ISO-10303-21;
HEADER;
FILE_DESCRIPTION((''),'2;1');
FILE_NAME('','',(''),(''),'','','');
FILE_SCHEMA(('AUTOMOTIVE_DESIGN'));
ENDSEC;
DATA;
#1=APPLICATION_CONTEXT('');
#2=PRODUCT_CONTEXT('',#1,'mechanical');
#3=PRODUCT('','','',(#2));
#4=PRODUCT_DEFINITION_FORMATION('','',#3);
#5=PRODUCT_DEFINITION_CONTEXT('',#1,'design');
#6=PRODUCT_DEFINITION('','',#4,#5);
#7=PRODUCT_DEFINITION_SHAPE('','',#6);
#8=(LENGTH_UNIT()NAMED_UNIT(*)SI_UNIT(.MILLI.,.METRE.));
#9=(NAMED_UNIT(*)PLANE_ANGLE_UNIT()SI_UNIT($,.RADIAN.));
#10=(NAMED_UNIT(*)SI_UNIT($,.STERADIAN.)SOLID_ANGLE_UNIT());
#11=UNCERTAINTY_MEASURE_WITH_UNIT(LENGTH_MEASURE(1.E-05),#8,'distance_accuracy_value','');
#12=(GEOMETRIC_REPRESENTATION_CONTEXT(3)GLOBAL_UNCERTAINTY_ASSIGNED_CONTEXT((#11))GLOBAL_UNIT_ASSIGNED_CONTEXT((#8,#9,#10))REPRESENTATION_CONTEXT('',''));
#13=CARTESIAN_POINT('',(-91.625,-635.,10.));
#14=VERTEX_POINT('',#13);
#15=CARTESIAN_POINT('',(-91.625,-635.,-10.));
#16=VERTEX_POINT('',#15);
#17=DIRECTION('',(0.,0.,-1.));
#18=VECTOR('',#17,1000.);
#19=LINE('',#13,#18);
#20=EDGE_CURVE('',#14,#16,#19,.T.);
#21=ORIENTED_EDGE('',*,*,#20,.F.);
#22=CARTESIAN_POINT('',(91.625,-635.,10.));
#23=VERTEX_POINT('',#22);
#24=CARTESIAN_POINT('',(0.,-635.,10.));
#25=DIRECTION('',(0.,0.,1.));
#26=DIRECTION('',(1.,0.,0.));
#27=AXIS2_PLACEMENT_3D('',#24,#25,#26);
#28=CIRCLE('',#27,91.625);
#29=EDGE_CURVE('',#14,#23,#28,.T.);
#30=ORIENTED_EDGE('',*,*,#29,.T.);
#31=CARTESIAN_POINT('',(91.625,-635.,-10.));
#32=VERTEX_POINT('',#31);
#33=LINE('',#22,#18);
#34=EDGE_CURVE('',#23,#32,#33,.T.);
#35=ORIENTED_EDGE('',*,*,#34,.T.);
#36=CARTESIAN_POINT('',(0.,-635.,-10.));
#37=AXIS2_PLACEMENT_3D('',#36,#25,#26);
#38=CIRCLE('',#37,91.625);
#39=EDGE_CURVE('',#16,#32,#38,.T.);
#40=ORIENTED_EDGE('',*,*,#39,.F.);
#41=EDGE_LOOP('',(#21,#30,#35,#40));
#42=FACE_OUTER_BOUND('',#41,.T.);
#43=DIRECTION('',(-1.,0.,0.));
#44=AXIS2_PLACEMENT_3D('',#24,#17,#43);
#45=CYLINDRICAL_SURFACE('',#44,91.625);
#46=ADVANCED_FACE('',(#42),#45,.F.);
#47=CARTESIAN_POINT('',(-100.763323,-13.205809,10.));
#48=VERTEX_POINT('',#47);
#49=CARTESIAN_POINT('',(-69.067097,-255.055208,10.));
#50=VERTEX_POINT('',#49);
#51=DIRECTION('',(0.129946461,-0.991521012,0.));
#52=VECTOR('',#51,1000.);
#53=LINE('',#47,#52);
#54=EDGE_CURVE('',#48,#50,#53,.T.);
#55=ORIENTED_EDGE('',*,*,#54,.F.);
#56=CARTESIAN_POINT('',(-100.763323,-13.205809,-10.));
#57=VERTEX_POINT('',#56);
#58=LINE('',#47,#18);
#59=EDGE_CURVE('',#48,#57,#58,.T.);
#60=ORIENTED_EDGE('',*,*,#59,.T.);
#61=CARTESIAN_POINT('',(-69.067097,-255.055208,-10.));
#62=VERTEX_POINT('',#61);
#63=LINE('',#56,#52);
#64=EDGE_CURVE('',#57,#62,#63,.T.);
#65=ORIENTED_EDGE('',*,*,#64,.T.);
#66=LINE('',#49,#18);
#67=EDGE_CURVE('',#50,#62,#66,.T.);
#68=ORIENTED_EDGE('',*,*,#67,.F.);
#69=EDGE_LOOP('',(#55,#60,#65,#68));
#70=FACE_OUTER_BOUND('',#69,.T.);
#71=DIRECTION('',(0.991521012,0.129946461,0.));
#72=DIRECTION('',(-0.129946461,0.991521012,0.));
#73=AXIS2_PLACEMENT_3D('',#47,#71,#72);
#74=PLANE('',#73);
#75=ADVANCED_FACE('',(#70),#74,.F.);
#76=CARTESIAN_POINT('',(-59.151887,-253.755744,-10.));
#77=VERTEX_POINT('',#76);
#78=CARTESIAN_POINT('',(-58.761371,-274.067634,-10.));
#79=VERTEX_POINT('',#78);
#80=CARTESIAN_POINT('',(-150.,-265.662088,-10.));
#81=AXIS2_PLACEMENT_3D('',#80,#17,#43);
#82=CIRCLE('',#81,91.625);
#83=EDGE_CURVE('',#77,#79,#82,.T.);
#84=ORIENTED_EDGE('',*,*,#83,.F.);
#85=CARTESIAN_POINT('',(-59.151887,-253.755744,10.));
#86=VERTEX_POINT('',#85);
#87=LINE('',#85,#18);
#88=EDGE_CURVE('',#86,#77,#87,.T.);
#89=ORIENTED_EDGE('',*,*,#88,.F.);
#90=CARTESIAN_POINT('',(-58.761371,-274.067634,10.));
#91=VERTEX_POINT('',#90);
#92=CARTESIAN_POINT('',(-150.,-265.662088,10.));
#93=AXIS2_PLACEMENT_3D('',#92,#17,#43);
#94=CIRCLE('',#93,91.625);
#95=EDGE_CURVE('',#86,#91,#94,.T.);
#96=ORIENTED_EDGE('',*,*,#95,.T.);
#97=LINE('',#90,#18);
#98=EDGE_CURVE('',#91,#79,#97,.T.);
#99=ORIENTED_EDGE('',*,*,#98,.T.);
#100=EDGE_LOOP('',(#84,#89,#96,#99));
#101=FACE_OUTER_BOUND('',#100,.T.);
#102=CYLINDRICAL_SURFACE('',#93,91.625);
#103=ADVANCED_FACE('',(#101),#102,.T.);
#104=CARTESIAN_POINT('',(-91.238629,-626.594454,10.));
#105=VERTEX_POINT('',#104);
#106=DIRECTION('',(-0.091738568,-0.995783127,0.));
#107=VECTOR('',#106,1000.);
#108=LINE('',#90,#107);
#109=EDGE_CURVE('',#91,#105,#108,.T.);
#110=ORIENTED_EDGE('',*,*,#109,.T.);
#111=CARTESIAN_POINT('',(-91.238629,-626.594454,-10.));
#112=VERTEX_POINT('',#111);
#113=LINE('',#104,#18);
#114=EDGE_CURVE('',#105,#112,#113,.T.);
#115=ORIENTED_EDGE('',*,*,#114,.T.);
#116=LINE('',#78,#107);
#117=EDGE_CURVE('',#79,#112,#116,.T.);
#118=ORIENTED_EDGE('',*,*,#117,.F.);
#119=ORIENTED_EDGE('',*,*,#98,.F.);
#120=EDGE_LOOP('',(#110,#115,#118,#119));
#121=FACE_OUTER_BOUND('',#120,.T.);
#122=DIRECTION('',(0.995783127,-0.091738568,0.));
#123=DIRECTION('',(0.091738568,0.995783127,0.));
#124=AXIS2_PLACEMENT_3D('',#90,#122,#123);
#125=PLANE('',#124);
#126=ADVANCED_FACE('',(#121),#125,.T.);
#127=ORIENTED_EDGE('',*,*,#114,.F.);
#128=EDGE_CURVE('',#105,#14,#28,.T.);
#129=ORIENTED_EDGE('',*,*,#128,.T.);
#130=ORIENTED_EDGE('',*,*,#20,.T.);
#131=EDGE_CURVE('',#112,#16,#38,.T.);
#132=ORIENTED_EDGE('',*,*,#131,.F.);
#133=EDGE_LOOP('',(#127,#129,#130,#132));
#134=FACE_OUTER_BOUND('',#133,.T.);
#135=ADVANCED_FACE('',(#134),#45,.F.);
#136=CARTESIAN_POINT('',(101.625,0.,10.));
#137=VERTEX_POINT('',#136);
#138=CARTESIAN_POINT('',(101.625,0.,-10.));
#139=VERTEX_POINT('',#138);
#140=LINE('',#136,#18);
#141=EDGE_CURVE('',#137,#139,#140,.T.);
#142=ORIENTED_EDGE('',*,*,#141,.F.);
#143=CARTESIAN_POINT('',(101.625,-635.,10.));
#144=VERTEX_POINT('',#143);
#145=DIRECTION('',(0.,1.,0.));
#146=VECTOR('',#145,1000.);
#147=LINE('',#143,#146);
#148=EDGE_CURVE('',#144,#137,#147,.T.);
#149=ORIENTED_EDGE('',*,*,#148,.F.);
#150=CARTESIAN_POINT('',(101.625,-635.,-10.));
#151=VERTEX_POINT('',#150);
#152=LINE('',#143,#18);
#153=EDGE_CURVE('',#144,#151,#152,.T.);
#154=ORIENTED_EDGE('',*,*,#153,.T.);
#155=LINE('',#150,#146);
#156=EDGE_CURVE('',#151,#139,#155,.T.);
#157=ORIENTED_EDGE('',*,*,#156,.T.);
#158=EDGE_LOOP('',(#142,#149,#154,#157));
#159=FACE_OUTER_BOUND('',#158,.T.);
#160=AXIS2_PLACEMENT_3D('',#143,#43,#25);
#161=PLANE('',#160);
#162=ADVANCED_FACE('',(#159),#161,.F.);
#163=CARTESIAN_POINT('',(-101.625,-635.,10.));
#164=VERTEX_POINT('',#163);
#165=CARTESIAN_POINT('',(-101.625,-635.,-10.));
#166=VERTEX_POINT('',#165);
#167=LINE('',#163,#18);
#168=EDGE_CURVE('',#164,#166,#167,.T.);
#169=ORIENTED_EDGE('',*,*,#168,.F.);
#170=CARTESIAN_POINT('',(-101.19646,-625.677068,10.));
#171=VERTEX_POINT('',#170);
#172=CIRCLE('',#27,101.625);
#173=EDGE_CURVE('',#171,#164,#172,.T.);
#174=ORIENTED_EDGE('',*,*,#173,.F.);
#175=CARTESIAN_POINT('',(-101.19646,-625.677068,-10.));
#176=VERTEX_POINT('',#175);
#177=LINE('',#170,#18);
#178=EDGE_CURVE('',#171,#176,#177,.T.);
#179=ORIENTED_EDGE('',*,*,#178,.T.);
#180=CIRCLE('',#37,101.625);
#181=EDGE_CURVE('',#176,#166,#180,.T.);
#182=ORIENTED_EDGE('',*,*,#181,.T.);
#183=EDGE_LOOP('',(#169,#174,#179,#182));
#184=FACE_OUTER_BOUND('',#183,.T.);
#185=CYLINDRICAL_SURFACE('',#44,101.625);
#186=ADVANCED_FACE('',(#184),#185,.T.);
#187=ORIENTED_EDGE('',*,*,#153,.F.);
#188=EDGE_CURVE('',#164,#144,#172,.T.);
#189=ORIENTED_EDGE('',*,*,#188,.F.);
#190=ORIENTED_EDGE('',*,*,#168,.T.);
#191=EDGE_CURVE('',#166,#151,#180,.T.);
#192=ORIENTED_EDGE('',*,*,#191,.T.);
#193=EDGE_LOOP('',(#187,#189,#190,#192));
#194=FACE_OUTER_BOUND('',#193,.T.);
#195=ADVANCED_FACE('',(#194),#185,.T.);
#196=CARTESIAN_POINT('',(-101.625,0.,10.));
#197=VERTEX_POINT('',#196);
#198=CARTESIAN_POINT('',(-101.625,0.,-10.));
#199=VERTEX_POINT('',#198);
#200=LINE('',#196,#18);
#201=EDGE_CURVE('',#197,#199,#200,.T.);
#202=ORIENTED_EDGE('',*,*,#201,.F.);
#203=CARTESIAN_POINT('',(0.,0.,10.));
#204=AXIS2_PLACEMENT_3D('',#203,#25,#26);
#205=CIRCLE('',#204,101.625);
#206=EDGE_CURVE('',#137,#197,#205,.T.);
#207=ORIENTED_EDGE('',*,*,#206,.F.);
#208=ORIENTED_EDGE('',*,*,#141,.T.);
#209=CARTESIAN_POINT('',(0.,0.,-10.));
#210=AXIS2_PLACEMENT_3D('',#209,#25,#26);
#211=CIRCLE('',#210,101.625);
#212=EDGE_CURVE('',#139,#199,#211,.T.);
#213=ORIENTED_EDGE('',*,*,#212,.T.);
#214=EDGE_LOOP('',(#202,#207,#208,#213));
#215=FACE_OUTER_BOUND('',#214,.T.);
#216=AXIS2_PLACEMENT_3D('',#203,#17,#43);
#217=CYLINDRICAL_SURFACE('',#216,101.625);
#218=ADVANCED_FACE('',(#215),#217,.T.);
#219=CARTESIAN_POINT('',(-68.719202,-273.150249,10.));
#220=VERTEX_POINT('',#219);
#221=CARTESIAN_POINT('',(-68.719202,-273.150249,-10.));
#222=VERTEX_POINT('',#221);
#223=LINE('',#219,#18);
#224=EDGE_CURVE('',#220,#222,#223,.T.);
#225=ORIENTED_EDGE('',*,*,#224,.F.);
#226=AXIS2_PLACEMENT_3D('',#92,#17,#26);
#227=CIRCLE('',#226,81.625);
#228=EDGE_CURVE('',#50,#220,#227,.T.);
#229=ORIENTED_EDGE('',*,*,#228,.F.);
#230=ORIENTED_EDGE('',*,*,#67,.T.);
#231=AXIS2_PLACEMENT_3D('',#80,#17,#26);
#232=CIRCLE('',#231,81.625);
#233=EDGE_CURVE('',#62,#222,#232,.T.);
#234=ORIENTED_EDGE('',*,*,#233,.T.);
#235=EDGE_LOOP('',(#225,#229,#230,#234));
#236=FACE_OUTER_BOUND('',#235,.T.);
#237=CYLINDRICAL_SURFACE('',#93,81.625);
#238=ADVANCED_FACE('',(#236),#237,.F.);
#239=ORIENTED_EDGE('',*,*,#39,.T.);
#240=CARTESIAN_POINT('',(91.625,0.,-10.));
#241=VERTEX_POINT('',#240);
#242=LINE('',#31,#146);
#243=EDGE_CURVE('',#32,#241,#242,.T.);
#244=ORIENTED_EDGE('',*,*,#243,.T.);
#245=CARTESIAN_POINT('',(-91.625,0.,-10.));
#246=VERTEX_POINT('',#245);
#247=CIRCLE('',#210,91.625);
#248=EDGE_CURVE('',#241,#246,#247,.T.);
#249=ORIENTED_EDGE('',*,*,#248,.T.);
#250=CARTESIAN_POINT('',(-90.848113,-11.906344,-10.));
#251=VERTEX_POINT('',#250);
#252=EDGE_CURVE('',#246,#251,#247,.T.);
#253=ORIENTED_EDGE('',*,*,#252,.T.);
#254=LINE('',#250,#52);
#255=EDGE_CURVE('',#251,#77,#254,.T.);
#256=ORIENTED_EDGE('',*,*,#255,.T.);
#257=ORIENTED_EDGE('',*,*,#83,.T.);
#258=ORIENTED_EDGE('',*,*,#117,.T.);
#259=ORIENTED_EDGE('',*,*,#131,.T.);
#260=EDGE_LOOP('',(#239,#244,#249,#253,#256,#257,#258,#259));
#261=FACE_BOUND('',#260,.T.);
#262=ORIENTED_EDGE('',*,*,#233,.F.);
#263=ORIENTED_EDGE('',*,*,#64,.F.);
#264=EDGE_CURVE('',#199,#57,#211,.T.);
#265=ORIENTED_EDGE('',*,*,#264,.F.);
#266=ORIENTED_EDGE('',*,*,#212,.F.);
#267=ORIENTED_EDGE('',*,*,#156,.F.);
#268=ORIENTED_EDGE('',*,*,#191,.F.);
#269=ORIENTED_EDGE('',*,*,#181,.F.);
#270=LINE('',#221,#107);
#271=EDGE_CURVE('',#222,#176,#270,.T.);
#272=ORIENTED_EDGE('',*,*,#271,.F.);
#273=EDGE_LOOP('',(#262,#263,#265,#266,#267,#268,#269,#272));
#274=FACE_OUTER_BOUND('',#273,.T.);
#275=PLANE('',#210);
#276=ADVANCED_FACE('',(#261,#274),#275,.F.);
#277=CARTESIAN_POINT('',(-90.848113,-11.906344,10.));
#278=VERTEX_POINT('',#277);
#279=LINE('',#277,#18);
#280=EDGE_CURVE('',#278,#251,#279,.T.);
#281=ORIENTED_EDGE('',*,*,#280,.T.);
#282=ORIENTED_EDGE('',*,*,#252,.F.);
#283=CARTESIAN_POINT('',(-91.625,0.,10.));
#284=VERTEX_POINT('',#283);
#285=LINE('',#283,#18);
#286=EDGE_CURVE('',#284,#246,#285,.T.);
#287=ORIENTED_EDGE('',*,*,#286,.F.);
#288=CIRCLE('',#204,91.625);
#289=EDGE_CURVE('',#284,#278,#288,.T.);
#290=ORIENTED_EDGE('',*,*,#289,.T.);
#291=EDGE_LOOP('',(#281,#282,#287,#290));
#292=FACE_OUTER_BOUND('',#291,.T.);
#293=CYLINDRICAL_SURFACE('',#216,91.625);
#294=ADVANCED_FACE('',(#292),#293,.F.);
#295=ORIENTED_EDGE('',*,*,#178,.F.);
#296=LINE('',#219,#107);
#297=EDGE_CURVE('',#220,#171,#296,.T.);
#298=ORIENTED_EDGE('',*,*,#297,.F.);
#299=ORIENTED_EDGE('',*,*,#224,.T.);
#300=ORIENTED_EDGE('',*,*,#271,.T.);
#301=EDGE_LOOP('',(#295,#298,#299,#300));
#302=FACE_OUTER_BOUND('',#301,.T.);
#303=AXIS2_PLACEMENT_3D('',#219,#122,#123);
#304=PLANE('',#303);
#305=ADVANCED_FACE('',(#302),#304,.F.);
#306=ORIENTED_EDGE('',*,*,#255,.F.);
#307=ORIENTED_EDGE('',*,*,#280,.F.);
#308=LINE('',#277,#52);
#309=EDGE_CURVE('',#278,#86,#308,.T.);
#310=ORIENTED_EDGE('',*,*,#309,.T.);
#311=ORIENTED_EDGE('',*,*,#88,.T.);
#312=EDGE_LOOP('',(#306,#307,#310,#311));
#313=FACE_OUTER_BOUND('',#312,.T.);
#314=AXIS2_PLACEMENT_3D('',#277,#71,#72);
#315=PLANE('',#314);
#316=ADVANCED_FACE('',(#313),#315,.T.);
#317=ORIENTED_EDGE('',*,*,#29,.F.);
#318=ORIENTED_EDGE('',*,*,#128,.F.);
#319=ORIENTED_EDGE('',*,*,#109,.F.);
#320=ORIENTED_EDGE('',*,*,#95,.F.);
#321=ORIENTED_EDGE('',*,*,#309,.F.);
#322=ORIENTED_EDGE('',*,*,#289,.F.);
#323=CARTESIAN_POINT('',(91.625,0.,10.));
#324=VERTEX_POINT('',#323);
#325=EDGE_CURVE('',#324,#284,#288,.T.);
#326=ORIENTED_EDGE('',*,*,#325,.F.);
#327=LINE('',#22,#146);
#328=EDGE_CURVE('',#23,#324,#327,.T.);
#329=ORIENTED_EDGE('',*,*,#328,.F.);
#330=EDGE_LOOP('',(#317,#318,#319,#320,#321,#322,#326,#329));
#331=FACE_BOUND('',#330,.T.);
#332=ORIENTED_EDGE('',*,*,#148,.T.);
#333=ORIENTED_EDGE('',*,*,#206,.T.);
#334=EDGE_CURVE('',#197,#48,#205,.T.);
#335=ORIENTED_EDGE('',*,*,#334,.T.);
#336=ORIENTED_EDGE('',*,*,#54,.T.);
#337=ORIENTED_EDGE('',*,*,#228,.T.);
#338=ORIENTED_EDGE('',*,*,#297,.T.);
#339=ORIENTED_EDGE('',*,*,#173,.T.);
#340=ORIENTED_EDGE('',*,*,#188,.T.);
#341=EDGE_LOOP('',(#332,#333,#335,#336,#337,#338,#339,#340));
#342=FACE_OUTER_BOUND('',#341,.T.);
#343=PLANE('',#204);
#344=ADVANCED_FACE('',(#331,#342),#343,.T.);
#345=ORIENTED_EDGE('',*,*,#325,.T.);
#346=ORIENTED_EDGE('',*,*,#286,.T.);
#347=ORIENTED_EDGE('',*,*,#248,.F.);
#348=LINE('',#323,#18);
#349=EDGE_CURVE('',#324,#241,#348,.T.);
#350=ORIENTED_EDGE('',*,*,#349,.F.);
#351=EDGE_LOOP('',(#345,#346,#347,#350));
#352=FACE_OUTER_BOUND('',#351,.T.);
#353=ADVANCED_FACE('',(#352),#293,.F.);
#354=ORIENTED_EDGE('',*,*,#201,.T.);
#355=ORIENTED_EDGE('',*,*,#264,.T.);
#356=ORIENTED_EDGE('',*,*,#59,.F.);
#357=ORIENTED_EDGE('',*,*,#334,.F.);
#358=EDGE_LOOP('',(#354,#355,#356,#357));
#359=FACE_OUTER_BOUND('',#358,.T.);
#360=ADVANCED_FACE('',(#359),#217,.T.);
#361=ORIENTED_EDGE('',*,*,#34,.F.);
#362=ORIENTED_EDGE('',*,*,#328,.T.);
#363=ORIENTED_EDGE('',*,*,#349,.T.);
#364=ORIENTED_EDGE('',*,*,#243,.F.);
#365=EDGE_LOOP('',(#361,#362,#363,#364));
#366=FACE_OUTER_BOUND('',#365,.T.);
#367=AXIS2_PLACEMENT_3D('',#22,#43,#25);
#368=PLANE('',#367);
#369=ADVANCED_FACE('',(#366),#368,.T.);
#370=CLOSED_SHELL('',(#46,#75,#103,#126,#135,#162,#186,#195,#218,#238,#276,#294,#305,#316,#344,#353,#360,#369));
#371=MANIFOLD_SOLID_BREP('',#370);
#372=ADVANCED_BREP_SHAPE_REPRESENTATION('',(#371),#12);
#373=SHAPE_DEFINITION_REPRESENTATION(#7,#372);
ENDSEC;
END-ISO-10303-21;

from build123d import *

# Parameters (mm, degrees)
EXTRUDE_1_DEPTH = 10


with BuildPart() as part:
    # 草图2 → 拉伸-薄壁1 (new, symmetric)
    with BuildSketch(Plane.XY):
        with BuildLine():
            Line((101.625, -635), (101.625, -1e-09))
            ThreePointArc((101.625, -2e-09), (-6.6169457, 101.409351915), (-100.763322845, -13.205809105))
            Line((-100.763322845, -13.205809104), (-69.067097403, -255.055208275))
            ThreePointArc((-69.067097403, -255.055208275), (-68.39008171, -264.093056524), (-68.7192023, -273.15024874))
            Line((-68.7192023, -273.15024874), (-101.19646024, -625.677068065))
            ThreePointArc((-101.19646024, -625.677068065), (-4.666387955, -736.517808529), (101.625, -635))
        make_face()
        with BuildLine():
            Line((91.625, -635), (91.625, -1e-09))
            ThreePointArc((91.625, -1e-09), (-5.965831732, 91.430571899), (-90.848112725, -11.906344494))
            Line((-90.848112725, -11.906344494), (-59.151887283, -253.755743665))
            ThreePointArc((-59.151887283, -253.755743665), (-58.391929391, -263.900832127), (-58.761371034, -274.067634416))
            Line((-58.761371034, -274.067634416), (-91.238628974, -626.594453741))
            ThreePointArc((-91.238628974, -626.594453741), (-4.207210789, -726.528356275), (91.625, -635))
        make_face(mode=Mode.SUBTRACT)
    extrude(amount=EXTRUDE_1_DEPTH, both=True)


solid = part.part
